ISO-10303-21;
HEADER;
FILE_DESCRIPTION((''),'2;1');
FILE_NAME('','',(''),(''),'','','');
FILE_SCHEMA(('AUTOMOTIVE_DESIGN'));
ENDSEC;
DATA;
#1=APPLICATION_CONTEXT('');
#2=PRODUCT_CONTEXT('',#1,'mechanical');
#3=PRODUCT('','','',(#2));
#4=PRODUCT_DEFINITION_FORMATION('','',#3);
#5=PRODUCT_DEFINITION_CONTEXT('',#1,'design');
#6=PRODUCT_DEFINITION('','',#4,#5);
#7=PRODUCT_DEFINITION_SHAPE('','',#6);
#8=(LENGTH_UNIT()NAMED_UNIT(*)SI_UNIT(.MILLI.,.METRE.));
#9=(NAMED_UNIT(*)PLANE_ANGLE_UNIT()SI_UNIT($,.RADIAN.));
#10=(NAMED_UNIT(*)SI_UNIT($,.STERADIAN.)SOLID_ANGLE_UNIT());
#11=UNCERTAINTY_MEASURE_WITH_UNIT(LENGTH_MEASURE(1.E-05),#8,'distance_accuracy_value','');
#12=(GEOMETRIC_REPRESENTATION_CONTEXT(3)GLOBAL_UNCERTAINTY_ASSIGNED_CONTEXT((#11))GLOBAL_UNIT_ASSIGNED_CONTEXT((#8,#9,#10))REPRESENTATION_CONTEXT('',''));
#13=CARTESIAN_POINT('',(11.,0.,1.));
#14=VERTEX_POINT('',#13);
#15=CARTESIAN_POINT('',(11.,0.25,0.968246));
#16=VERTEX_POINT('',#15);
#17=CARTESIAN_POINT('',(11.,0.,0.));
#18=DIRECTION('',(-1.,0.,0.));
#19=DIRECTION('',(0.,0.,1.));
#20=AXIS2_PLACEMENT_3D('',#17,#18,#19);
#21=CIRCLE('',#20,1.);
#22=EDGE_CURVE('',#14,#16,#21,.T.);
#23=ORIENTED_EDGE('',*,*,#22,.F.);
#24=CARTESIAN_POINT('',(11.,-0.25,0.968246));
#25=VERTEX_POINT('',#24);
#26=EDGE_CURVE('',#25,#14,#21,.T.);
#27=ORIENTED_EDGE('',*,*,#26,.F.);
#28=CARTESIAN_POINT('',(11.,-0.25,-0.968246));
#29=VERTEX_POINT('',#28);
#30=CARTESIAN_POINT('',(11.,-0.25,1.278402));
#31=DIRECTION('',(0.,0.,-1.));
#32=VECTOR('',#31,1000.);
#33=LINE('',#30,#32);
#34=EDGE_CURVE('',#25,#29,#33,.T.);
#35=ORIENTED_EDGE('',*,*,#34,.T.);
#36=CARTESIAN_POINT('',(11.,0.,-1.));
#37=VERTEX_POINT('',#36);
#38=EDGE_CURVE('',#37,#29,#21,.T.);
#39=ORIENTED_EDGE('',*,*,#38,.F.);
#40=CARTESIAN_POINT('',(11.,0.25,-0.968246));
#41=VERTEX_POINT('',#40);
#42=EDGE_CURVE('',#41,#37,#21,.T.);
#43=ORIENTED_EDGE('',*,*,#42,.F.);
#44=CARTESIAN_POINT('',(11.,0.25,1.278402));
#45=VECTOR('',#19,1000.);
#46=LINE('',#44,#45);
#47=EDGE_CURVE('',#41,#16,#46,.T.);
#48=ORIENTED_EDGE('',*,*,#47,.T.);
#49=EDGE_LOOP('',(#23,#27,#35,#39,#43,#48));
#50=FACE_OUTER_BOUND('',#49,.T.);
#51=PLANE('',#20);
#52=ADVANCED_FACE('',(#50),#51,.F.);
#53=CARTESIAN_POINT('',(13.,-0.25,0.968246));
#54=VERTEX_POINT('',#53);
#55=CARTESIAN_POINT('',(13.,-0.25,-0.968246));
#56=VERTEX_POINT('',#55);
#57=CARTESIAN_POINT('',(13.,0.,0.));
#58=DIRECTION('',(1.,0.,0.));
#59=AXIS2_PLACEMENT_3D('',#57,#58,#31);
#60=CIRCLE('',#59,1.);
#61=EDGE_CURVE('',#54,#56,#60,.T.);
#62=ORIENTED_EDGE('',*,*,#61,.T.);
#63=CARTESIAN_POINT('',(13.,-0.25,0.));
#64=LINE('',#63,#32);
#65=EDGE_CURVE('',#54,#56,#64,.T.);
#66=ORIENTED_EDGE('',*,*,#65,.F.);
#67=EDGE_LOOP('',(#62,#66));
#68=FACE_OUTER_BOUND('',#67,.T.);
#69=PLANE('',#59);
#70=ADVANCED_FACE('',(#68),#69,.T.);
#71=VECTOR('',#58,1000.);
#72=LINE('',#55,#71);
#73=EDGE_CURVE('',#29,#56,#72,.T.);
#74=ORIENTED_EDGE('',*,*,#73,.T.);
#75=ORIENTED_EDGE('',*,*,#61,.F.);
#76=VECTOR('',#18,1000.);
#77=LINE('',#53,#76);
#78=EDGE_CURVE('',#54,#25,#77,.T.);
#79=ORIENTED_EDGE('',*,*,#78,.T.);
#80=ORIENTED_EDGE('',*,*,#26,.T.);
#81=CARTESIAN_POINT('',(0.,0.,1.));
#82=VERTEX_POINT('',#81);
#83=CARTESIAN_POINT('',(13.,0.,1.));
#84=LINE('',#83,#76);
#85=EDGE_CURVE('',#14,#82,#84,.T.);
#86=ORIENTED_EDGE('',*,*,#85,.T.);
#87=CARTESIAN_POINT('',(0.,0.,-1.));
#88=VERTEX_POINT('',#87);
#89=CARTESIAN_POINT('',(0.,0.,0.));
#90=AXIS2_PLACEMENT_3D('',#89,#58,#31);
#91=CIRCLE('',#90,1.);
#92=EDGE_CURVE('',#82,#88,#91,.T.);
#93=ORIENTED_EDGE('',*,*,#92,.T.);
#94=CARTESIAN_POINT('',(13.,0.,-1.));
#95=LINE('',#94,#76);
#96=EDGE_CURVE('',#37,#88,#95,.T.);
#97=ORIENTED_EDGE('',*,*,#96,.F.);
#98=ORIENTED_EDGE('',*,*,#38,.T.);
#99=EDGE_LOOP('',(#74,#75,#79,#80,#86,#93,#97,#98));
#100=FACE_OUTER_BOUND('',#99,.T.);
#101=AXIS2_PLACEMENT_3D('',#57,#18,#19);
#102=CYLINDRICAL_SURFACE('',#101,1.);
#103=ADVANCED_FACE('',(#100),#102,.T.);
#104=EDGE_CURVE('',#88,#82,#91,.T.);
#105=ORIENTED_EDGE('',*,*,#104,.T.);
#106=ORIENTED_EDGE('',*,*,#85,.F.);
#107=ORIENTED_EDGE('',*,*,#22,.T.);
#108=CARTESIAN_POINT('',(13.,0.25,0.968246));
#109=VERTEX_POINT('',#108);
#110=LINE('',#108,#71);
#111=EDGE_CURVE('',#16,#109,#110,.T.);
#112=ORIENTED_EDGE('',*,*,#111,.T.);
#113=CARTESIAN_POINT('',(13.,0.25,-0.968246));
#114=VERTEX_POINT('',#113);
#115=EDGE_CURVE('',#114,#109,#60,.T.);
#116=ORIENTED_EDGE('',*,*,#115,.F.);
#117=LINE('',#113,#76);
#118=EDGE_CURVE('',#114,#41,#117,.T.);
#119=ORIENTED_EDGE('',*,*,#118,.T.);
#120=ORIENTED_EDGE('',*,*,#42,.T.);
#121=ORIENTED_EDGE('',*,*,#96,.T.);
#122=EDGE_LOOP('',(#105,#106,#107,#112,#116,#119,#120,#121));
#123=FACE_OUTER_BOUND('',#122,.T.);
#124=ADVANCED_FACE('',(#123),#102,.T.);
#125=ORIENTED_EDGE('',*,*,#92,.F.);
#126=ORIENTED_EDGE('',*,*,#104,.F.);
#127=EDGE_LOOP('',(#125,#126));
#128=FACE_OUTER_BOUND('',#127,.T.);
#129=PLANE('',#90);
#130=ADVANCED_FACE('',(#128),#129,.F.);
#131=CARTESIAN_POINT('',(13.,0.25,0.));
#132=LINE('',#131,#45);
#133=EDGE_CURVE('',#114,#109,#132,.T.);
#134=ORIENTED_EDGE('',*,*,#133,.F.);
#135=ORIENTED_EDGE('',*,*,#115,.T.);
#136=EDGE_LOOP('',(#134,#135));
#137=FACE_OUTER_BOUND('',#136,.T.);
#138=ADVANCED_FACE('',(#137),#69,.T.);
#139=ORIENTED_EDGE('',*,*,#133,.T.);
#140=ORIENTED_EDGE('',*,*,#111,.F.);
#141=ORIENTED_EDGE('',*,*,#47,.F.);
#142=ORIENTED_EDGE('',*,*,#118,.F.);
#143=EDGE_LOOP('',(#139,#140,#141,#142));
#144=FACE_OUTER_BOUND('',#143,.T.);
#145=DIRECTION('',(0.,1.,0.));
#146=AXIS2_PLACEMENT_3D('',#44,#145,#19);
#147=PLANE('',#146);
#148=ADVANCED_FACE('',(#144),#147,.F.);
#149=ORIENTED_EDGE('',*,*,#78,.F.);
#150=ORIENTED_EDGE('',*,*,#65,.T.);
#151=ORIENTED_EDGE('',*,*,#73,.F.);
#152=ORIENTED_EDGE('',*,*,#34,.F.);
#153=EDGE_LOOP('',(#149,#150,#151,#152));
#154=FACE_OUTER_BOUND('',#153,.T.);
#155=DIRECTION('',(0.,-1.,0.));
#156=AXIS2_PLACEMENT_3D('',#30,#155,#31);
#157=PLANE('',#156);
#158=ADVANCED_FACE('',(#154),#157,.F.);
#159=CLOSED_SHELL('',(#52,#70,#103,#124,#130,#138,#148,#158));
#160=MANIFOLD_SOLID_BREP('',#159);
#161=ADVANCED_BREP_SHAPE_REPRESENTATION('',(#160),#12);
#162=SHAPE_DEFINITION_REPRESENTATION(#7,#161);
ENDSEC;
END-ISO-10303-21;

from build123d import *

# Parameters (mm, degrees)
SKETCH1_R           = 1
BOSS_EXTRUDE1_DEPTH = 13
SKETCH2_W           = 2.556803996
SKETCH2_H           = 0.5
CUT_EXTRUDE1_DEPTH  = 2


with BuildPart() as part:
    # Sketch1 → Boss-Extrude1 (new body)
    with BuildSketch(Plane(origin=(0, 0, 0), x_dir=(0, 0, -1), z_dir=(1, 0, 0))):
        with Locations(Location((0, 0, 0), (0, 0, 180))):
            Circle(SKETCH1_R)
    extrude(amount=BOSS_EXTRUDE1_DEPTH)

    # Sketch2 → Cut-Extrude1 (cut)
    with BuildSketch(Plane(origin=(13, 0, 0), x_dir=(0, 0, -1), z_dir=(1, 0, 0))):
        Rectangle(SKETCH2_W, SKETCH2_H)
    extrude(amount=-CUT_EXTRUDE1_DEPTH, mode=Mode.SUBTRACT)


solid = part.part
